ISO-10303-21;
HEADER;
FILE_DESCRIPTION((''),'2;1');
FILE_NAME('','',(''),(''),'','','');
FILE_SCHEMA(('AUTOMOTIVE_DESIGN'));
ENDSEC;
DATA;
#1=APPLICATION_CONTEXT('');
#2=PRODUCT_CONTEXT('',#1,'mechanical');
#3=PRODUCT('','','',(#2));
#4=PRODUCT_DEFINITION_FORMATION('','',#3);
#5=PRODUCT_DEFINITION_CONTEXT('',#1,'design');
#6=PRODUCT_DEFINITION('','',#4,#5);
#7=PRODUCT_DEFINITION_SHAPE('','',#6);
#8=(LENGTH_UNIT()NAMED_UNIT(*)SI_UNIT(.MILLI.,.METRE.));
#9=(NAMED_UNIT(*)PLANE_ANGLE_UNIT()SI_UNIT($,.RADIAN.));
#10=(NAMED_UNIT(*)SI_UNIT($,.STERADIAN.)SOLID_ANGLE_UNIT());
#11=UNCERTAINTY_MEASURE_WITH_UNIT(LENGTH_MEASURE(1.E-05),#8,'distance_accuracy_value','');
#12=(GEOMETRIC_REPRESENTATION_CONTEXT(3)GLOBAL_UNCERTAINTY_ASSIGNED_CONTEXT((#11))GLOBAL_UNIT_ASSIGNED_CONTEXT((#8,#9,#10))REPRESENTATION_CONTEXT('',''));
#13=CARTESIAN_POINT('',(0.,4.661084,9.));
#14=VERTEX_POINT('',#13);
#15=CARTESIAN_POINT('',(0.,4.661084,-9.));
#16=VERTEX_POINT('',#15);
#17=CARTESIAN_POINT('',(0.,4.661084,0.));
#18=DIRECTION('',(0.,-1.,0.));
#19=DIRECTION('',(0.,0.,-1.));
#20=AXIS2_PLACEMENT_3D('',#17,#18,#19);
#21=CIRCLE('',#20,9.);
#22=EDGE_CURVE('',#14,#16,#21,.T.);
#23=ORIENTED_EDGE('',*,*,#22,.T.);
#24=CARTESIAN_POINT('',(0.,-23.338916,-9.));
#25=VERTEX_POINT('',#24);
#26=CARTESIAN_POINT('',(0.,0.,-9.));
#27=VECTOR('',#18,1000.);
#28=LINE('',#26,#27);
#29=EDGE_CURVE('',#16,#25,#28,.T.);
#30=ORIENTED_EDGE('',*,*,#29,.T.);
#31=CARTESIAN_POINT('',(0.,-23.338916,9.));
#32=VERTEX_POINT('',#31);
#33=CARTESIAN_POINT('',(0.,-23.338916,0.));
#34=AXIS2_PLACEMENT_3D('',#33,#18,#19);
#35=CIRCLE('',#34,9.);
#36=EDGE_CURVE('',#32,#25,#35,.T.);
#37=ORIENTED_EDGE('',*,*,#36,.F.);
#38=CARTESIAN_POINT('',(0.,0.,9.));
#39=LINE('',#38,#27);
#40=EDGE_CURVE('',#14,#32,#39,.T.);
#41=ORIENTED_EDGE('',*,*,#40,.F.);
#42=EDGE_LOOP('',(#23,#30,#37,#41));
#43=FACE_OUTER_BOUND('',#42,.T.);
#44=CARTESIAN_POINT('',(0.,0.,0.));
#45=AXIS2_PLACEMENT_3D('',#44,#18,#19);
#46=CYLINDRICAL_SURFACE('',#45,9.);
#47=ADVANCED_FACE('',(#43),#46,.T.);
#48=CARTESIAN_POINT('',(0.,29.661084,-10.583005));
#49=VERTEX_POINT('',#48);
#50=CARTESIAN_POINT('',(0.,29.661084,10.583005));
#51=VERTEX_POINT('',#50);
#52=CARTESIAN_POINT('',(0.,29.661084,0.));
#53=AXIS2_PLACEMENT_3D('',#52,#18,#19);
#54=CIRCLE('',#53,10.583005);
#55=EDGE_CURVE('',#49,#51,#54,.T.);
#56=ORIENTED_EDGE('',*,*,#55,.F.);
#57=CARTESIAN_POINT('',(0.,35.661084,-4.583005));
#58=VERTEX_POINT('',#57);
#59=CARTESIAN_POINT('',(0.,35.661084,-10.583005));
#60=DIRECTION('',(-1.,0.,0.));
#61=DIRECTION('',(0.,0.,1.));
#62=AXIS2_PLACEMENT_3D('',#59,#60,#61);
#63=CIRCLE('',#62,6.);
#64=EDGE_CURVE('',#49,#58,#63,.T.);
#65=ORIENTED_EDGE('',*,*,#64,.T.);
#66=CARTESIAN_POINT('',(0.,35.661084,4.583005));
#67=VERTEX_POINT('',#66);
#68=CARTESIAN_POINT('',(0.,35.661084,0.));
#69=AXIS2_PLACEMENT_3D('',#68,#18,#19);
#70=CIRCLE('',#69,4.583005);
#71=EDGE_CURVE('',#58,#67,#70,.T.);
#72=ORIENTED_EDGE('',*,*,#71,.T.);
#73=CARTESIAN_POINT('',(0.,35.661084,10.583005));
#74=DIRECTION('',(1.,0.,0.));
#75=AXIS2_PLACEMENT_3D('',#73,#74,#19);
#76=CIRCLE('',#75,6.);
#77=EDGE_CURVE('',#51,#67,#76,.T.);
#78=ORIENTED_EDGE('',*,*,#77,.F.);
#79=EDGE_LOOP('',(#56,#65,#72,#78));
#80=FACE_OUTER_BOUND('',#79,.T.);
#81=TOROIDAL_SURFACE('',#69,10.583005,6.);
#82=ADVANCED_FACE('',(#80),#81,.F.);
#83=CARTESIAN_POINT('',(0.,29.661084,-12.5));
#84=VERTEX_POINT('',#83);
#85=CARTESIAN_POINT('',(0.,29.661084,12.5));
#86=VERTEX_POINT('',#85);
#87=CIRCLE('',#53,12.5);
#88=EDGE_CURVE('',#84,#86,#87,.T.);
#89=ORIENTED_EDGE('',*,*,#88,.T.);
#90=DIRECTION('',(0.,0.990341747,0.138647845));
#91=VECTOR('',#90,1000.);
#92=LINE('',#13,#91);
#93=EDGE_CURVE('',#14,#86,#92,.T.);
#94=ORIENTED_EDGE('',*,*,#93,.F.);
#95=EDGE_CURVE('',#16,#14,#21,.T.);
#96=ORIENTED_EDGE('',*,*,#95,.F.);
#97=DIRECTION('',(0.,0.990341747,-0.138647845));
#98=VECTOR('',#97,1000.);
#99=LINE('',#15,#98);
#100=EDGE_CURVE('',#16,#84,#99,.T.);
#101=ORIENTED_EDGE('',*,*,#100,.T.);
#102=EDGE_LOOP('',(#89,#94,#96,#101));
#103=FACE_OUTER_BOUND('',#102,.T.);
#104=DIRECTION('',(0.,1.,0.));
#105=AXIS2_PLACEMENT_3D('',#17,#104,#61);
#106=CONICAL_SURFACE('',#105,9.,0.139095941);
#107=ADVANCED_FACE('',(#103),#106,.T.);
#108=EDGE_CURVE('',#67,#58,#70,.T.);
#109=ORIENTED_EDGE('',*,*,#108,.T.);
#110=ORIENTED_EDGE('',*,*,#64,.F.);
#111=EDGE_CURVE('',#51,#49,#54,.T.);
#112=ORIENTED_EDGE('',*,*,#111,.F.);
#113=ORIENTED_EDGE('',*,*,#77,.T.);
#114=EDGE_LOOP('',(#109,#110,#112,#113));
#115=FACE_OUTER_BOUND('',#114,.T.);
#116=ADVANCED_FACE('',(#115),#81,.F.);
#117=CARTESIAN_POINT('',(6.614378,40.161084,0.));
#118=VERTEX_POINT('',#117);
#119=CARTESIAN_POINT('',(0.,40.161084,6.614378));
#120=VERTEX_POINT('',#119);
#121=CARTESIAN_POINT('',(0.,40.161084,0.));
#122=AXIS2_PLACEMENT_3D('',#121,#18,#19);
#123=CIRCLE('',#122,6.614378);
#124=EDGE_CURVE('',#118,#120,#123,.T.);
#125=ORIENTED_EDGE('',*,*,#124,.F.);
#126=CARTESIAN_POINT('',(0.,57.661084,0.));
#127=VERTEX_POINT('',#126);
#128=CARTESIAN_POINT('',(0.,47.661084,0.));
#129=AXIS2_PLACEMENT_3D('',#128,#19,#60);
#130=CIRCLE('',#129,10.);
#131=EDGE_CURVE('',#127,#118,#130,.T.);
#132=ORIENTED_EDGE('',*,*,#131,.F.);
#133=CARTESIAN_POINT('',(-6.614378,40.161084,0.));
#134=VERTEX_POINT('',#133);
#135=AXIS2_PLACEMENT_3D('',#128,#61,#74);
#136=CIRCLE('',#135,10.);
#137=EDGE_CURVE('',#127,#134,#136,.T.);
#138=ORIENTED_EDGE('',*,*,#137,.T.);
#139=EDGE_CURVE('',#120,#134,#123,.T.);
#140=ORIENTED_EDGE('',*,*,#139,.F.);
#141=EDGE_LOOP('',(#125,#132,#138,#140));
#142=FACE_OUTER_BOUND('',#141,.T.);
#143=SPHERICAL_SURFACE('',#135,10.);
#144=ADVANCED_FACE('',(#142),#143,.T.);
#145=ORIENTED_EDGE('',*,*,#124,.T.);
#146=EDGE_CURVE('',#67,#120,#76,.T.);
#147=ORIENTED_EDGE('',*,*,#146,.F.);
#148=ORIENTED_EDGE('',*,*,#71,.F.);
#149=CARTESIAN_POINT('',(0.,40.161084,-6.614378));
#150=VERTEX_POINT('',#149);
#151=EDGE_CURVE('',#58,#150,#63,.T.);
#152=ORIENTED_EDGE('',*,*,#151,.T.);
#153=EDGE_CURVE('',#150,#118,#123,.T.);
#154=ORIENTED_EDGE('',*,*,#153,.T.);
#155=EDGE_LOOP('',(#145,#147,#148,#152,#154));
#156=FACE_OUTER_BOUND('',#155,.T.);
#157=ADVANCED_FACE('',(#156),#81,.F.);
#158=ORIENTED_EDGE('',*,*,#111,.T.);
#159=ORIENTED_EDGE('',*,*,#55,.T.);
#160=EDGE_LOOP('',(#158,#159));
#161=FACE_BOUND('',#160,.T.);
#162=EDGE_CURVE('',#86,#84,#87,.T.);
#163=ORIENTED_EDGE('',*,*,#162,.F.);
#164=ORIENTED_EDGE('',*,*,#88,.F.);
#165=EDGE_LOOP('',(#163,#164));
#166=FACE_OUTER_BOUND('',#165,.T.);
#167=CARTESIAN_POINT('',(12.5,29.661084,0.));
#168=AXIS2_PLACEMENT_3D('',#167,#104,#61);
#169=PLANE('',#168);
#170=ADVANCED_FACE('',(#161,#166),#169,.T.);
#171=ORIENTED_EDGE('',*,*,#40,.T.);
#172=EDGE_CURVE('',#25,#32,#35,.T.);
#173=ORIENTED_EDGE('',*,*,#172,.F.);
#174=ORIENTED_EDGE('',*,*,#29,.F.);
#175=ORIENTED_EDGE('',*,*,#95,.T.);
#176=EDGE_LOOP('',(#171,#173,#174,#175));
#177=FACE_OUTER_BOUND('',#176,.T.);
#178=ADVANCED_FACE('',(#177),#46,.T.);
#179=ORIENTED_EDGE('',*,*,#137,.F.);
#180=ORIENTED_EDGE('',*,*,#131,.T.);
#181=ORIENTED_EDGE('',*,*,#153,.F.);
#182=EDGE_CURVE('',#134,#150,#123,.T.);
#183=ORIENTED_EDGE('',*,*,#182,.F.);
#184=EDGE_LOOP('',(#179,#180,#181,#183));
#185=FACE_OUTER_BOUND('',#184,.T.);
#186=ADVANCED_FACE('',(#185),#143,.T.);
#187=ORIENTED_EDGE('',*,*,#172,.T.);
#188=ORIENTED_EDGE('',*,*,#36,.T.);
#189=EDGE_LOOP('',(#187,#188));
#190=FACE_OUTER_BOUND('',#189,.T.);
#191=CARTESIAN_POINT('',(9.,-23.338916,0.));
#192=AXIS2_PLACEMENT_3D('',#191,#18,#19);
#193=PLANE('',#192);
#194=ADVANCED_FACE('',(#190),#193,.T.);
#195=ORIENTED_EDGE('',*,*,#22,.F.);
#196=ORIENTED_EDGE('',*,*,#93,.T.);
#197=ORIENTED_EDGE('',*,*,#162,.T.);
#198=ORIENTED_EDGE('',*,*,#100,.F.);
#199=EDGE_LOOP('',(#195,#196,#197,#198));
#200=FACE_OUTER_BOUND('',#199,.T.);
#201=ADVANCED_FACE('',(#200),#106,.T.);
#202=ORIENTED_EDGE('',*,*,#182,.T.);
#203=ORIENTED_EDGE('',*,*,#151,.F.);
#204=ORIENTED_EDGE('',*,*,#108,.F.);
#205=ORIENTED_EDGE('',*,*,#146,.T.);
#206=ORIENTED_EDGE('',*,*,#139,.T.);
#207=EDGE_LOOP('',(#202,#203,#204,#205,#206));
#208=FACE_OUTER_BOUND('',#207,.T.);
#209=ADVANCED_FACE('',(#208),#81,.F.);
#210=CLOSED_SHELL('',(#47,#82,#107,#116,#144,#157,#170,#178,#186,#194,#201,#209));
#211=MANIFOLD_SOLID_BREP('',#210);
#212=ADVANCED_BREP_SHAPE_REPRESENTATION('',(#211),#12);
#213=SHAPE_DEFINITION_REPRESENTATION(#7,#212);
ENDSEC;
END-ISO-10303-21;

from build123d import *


with BuildPart() as part:
    # Pin Profile Sketch → Pin Body Revolve (revolve)
    with BuildSketch(Plane.XY, mode=Mode.PRIVATE) as pin_body_revolve_sk:
        with BuildLine():
            Line((9, 4.661084251), (12.5, 29.661084251))
            Line((12.5, 29.661084251), (10.583005244, 29.661084251))
            ThreePointArc((10.583005244, 29.661084251), (4.970519164, 33.539763908), (6.614378278, 40.161084251))
            ThreePointArc((6.614378278, 40.161084251), (9.354143467, 51.196618157), (0, 57.661084251))
            Line((0, 57.661084251), (0, 29.661084251))
            Line((0, 29.661084251), (0, 0))
            Line((0, 0), (0, -23.338915749))
            Line((0, -23.338915749), (9, -23.338915749))
            Line((9, -23.338915749), (9, 4.661084251))
        make_face()
    revolve(pin_body_revolve_sk.sketch.rotate(Axis((0, 0, 0), (0, 1, 0)), 90), axis=Axis((0, 0, 0), (0, 1, 0)))


solid = part.part
